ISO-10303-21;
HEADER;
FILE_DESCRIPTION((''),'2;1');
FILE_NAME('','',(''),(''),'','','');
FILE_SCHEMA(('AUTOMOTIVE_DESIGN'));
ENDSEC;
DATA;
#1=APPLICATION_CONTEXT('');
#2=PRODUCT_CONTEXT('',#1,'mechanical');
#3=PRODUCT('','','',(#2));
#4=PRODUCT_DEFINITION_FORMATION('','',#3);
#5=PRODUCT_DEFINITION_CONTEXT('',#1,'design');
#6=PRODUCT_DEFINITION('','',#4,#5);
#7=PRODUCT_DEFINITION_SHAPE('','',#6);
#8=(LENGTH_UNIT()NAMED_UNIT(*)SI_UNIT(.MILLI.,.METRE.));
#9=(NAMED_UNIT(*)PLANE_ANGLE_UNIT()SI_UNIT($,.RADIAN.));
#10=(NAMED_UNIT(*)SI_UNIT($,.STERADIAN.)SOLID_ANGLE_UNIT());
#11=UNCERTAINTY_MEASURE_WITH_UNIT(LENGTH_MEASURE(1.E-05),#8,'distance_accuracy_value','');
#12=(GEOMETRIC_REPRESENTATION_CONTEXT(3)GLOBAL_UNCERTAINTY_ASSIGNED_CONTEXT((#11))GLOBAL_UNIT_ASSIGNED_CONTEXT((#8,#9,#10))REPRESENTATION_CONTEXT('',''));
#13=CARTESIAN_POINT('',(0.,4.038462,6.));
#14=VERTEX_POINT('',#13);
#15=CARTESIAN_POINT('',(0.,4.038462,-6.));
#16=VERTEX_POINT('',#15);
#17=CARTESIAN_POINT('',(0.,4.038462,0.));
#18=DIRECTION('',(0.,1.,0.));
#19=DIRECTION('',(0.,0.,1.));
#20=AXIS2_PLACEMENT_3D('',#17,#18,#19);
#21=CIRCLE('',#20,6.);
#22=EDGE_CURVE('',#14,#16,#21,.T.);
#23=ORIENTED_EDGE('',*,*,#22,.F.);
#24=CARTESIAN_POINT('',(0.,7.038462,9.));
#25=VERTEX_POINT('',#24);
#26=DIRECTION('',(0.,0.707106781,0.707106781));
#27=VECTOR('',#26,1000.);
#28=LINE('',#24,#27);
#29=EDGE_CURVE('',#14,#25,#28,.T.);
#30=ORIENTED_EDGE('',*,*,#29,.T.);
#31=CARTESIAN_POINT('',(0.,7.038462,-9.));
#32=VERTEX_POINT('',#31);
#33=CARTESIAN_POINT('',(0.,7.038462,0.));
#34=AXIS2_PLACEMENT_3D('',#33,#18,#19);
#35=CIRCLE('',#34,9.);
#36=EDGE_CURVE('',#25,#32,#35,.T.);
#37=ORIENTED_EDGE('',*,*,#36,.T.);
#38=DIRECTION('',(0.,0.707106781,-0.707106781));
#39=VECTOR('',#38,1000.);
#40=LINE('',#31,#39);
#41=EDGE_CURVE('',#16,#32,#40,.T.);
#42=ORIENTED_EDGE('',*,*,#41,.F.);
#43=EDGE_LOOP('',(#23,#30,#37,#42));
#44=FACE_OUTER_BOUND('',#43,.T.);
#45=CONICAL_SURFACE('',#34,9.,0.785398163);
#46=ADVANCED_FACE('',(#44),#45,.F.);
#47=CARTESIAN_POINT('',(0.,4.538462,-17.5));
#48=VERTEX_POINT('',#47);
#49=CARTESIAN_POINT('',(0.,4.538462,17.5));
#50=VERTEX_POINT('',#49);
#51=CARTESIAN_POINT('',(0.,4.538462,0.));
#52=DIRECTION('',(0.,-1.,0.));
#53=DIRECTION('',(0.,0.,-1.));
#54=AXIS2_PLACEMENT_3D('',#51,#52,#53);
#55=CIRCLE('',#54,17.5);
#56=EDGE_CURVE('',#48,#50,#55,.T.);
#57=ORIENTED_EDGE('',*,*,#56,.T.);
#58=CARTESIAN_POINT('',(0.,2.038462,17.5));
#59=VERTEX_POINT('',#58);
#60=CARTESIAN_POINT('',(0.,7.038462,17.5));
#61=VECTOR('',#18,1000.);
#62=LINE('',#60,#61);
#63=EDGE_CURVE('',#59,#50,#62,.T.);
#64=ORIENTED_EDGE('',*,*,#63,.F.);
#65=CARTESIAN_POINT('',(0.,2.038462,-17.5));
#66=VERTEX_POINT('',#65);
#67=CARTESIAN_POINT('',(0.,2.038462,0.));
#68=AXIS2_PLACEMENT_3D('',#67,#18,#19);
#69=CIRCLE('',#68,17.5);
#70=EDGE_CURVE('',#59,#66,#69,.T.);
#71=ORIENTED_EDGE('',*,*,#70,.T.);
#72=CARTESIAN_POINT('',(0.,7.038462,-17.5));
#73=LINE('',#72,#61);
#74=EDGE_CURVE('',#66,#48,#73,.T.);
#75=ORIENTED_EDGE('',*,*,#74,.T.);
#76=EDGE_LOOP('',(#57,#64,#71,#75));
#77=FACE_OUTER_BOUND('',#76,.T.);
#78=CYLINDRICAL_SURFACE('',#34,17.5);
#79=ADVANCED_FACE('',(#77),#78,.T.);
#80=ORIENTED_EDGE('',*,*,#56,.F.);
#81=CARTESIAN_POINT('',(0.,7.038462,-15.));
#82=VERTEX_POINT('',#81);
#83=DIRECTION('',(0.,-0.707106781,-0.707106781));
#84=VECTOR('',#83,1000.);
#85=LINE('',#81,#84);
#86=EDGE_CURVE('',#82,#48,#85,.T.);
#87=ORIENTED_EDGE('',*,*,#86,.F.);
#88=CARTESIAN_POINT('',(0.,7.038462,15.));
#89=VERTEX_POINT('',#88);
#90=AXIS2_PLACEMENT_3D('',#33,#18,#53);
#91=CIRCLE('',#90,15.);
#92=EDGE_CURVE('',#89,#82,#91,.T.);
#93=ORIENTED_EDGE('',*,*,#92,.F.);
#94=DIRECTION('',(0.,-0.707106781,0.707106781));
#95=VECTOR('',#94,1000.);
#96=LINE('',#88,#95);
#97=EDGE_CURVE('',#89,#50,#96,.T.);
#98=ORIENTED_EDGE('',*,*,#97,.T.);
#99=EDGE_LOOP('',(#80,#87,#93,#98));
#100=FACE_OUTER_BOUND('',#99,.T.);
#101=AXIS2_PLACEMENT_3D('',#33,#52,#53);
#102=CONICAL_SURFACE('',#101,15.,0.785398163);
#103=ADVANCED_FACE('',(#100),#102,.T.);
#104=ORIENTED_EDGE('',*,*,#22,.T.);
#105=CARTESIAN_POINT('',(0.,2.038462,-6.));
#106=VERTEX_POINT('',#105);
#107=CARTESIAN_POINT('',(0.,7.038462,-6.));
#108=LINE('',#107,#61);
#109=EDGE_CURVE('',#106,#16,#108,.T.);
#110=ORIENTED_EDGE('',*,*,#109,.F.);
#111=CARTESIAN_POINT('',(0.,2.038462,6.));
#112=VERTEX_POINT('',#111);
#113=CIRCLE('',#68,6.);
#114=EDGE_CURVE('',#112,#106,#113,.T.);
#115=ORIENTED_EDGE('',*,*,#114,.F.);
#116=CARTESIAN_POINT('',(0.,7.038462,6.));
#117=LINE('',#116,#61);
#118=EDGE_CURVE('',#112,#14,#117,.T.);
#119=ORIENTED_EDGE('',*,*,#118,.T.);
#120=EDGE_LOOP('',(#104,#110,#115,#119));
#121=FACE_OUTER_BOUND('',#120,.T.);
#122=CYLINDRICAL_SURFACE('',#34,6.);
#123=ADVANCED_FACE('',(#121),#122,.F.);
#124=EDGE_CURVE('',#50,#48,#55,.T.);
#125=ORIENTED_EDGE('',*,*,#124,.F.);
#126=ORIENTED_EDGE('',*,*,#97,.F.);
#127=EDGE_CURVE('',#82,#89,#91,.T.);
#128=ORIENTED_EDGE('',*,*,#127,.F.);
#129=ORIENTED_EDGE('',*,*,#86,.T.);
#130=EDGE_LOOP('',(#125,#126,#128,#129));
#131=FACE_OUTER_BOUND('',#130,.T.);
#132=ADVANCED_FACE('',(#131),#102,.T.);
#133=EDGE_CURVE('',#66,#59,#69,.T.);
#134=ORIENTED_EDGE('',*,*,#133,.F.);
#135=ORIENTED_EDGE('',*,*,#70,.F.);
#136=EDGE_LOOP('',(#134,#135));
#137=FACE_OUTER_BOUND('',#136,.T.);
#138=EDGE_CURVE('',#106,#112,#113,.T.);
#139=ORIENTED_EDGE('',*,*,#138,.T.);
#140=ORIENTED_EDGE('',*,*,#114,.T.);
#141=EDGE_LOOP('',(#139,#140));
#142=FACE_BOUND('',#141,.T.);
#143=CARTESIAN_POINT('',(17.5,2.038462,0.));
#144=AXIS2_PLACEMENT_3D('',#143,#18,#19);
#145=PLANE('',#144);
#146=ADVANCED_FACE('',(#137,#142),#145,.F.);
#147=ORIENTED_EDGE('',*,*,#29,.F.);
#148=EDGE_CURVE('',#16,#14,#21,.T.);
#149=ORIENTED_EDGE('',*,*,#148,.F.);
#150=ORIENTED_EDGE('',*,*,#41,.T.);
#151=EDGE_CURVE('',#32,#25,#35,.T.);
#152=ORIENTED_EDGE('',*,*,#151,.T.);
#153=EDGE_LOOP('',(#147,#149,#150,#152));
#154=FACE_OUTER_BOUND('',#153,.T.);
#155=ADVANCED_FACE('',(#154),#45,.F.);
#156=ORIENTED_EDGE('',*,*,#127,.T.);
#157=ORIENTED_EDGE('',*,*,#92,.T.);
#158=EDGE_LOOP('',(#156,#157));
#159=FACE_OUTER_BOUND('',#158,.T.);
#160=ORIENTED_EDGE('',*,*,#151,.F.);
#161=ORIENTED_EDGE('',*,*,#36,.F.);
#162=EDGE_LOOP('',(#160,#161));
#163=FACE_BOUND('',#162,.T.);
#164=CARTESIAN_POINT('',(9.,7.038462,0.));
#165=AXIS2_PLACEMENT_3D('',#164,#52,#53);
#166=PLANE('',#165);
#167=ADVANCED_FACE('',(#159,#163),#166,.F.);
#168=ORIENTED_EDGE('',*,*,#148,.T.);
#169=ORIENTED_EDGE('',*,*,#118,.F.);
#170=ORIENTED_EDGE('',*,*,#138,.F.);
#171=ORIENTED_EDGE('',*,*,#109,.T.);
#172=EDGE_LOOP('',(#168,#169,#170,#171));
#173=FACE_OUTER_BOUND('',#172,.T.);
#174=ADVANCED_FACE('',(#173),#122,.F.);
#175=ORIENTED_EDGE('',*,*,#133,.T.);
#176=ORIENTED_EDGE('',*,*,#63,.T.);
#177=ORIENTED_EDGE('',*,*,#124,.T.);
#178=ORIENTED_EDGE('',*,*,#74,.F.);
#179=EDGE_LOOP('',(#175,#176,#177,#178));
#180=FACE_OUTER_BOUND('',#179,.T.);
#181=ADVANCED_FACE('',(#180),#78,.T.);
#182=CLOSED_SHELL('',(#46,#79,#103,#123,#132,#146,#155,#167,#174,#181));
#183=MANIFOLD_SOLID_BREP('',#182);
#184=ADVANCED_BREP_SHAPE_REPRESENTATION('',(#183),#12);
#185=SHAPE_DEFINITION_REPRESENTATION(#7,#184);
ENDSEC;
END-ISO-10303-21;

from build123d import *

# Parameters (mm, degrees)
CHAMFER1_SIZE = 2.5


with BuildPart() as part:
    # Sketch1 → Revolve1 (revolve)
    with BuildSketch(Plane.XY, mode=Mode.PRIVATE) as revolve1_sk:
        Polygon((9, 7.038461538), (17.5, 7.038461538), (17.5, 2.038461538), (6, 2.038461538), (6, 4.038461538), align=None)
    revolve(revolve1_sk.sketch.rotate(Axis((0, 7.038461538, 0), (0, -1, 0)), 90), axis=Axis((0, 7.038461538, 0), (0, -1, 0)))

    # Chamfer1
    chamfer1_edges = [part.edges().sort_by_distance(p)[0] for p in [
        (0, 7.038461538, -17.5),
    ]]
    chamfer(chamfer1_edges, length=CHAMFER1_SIZE)


solid = part.part
